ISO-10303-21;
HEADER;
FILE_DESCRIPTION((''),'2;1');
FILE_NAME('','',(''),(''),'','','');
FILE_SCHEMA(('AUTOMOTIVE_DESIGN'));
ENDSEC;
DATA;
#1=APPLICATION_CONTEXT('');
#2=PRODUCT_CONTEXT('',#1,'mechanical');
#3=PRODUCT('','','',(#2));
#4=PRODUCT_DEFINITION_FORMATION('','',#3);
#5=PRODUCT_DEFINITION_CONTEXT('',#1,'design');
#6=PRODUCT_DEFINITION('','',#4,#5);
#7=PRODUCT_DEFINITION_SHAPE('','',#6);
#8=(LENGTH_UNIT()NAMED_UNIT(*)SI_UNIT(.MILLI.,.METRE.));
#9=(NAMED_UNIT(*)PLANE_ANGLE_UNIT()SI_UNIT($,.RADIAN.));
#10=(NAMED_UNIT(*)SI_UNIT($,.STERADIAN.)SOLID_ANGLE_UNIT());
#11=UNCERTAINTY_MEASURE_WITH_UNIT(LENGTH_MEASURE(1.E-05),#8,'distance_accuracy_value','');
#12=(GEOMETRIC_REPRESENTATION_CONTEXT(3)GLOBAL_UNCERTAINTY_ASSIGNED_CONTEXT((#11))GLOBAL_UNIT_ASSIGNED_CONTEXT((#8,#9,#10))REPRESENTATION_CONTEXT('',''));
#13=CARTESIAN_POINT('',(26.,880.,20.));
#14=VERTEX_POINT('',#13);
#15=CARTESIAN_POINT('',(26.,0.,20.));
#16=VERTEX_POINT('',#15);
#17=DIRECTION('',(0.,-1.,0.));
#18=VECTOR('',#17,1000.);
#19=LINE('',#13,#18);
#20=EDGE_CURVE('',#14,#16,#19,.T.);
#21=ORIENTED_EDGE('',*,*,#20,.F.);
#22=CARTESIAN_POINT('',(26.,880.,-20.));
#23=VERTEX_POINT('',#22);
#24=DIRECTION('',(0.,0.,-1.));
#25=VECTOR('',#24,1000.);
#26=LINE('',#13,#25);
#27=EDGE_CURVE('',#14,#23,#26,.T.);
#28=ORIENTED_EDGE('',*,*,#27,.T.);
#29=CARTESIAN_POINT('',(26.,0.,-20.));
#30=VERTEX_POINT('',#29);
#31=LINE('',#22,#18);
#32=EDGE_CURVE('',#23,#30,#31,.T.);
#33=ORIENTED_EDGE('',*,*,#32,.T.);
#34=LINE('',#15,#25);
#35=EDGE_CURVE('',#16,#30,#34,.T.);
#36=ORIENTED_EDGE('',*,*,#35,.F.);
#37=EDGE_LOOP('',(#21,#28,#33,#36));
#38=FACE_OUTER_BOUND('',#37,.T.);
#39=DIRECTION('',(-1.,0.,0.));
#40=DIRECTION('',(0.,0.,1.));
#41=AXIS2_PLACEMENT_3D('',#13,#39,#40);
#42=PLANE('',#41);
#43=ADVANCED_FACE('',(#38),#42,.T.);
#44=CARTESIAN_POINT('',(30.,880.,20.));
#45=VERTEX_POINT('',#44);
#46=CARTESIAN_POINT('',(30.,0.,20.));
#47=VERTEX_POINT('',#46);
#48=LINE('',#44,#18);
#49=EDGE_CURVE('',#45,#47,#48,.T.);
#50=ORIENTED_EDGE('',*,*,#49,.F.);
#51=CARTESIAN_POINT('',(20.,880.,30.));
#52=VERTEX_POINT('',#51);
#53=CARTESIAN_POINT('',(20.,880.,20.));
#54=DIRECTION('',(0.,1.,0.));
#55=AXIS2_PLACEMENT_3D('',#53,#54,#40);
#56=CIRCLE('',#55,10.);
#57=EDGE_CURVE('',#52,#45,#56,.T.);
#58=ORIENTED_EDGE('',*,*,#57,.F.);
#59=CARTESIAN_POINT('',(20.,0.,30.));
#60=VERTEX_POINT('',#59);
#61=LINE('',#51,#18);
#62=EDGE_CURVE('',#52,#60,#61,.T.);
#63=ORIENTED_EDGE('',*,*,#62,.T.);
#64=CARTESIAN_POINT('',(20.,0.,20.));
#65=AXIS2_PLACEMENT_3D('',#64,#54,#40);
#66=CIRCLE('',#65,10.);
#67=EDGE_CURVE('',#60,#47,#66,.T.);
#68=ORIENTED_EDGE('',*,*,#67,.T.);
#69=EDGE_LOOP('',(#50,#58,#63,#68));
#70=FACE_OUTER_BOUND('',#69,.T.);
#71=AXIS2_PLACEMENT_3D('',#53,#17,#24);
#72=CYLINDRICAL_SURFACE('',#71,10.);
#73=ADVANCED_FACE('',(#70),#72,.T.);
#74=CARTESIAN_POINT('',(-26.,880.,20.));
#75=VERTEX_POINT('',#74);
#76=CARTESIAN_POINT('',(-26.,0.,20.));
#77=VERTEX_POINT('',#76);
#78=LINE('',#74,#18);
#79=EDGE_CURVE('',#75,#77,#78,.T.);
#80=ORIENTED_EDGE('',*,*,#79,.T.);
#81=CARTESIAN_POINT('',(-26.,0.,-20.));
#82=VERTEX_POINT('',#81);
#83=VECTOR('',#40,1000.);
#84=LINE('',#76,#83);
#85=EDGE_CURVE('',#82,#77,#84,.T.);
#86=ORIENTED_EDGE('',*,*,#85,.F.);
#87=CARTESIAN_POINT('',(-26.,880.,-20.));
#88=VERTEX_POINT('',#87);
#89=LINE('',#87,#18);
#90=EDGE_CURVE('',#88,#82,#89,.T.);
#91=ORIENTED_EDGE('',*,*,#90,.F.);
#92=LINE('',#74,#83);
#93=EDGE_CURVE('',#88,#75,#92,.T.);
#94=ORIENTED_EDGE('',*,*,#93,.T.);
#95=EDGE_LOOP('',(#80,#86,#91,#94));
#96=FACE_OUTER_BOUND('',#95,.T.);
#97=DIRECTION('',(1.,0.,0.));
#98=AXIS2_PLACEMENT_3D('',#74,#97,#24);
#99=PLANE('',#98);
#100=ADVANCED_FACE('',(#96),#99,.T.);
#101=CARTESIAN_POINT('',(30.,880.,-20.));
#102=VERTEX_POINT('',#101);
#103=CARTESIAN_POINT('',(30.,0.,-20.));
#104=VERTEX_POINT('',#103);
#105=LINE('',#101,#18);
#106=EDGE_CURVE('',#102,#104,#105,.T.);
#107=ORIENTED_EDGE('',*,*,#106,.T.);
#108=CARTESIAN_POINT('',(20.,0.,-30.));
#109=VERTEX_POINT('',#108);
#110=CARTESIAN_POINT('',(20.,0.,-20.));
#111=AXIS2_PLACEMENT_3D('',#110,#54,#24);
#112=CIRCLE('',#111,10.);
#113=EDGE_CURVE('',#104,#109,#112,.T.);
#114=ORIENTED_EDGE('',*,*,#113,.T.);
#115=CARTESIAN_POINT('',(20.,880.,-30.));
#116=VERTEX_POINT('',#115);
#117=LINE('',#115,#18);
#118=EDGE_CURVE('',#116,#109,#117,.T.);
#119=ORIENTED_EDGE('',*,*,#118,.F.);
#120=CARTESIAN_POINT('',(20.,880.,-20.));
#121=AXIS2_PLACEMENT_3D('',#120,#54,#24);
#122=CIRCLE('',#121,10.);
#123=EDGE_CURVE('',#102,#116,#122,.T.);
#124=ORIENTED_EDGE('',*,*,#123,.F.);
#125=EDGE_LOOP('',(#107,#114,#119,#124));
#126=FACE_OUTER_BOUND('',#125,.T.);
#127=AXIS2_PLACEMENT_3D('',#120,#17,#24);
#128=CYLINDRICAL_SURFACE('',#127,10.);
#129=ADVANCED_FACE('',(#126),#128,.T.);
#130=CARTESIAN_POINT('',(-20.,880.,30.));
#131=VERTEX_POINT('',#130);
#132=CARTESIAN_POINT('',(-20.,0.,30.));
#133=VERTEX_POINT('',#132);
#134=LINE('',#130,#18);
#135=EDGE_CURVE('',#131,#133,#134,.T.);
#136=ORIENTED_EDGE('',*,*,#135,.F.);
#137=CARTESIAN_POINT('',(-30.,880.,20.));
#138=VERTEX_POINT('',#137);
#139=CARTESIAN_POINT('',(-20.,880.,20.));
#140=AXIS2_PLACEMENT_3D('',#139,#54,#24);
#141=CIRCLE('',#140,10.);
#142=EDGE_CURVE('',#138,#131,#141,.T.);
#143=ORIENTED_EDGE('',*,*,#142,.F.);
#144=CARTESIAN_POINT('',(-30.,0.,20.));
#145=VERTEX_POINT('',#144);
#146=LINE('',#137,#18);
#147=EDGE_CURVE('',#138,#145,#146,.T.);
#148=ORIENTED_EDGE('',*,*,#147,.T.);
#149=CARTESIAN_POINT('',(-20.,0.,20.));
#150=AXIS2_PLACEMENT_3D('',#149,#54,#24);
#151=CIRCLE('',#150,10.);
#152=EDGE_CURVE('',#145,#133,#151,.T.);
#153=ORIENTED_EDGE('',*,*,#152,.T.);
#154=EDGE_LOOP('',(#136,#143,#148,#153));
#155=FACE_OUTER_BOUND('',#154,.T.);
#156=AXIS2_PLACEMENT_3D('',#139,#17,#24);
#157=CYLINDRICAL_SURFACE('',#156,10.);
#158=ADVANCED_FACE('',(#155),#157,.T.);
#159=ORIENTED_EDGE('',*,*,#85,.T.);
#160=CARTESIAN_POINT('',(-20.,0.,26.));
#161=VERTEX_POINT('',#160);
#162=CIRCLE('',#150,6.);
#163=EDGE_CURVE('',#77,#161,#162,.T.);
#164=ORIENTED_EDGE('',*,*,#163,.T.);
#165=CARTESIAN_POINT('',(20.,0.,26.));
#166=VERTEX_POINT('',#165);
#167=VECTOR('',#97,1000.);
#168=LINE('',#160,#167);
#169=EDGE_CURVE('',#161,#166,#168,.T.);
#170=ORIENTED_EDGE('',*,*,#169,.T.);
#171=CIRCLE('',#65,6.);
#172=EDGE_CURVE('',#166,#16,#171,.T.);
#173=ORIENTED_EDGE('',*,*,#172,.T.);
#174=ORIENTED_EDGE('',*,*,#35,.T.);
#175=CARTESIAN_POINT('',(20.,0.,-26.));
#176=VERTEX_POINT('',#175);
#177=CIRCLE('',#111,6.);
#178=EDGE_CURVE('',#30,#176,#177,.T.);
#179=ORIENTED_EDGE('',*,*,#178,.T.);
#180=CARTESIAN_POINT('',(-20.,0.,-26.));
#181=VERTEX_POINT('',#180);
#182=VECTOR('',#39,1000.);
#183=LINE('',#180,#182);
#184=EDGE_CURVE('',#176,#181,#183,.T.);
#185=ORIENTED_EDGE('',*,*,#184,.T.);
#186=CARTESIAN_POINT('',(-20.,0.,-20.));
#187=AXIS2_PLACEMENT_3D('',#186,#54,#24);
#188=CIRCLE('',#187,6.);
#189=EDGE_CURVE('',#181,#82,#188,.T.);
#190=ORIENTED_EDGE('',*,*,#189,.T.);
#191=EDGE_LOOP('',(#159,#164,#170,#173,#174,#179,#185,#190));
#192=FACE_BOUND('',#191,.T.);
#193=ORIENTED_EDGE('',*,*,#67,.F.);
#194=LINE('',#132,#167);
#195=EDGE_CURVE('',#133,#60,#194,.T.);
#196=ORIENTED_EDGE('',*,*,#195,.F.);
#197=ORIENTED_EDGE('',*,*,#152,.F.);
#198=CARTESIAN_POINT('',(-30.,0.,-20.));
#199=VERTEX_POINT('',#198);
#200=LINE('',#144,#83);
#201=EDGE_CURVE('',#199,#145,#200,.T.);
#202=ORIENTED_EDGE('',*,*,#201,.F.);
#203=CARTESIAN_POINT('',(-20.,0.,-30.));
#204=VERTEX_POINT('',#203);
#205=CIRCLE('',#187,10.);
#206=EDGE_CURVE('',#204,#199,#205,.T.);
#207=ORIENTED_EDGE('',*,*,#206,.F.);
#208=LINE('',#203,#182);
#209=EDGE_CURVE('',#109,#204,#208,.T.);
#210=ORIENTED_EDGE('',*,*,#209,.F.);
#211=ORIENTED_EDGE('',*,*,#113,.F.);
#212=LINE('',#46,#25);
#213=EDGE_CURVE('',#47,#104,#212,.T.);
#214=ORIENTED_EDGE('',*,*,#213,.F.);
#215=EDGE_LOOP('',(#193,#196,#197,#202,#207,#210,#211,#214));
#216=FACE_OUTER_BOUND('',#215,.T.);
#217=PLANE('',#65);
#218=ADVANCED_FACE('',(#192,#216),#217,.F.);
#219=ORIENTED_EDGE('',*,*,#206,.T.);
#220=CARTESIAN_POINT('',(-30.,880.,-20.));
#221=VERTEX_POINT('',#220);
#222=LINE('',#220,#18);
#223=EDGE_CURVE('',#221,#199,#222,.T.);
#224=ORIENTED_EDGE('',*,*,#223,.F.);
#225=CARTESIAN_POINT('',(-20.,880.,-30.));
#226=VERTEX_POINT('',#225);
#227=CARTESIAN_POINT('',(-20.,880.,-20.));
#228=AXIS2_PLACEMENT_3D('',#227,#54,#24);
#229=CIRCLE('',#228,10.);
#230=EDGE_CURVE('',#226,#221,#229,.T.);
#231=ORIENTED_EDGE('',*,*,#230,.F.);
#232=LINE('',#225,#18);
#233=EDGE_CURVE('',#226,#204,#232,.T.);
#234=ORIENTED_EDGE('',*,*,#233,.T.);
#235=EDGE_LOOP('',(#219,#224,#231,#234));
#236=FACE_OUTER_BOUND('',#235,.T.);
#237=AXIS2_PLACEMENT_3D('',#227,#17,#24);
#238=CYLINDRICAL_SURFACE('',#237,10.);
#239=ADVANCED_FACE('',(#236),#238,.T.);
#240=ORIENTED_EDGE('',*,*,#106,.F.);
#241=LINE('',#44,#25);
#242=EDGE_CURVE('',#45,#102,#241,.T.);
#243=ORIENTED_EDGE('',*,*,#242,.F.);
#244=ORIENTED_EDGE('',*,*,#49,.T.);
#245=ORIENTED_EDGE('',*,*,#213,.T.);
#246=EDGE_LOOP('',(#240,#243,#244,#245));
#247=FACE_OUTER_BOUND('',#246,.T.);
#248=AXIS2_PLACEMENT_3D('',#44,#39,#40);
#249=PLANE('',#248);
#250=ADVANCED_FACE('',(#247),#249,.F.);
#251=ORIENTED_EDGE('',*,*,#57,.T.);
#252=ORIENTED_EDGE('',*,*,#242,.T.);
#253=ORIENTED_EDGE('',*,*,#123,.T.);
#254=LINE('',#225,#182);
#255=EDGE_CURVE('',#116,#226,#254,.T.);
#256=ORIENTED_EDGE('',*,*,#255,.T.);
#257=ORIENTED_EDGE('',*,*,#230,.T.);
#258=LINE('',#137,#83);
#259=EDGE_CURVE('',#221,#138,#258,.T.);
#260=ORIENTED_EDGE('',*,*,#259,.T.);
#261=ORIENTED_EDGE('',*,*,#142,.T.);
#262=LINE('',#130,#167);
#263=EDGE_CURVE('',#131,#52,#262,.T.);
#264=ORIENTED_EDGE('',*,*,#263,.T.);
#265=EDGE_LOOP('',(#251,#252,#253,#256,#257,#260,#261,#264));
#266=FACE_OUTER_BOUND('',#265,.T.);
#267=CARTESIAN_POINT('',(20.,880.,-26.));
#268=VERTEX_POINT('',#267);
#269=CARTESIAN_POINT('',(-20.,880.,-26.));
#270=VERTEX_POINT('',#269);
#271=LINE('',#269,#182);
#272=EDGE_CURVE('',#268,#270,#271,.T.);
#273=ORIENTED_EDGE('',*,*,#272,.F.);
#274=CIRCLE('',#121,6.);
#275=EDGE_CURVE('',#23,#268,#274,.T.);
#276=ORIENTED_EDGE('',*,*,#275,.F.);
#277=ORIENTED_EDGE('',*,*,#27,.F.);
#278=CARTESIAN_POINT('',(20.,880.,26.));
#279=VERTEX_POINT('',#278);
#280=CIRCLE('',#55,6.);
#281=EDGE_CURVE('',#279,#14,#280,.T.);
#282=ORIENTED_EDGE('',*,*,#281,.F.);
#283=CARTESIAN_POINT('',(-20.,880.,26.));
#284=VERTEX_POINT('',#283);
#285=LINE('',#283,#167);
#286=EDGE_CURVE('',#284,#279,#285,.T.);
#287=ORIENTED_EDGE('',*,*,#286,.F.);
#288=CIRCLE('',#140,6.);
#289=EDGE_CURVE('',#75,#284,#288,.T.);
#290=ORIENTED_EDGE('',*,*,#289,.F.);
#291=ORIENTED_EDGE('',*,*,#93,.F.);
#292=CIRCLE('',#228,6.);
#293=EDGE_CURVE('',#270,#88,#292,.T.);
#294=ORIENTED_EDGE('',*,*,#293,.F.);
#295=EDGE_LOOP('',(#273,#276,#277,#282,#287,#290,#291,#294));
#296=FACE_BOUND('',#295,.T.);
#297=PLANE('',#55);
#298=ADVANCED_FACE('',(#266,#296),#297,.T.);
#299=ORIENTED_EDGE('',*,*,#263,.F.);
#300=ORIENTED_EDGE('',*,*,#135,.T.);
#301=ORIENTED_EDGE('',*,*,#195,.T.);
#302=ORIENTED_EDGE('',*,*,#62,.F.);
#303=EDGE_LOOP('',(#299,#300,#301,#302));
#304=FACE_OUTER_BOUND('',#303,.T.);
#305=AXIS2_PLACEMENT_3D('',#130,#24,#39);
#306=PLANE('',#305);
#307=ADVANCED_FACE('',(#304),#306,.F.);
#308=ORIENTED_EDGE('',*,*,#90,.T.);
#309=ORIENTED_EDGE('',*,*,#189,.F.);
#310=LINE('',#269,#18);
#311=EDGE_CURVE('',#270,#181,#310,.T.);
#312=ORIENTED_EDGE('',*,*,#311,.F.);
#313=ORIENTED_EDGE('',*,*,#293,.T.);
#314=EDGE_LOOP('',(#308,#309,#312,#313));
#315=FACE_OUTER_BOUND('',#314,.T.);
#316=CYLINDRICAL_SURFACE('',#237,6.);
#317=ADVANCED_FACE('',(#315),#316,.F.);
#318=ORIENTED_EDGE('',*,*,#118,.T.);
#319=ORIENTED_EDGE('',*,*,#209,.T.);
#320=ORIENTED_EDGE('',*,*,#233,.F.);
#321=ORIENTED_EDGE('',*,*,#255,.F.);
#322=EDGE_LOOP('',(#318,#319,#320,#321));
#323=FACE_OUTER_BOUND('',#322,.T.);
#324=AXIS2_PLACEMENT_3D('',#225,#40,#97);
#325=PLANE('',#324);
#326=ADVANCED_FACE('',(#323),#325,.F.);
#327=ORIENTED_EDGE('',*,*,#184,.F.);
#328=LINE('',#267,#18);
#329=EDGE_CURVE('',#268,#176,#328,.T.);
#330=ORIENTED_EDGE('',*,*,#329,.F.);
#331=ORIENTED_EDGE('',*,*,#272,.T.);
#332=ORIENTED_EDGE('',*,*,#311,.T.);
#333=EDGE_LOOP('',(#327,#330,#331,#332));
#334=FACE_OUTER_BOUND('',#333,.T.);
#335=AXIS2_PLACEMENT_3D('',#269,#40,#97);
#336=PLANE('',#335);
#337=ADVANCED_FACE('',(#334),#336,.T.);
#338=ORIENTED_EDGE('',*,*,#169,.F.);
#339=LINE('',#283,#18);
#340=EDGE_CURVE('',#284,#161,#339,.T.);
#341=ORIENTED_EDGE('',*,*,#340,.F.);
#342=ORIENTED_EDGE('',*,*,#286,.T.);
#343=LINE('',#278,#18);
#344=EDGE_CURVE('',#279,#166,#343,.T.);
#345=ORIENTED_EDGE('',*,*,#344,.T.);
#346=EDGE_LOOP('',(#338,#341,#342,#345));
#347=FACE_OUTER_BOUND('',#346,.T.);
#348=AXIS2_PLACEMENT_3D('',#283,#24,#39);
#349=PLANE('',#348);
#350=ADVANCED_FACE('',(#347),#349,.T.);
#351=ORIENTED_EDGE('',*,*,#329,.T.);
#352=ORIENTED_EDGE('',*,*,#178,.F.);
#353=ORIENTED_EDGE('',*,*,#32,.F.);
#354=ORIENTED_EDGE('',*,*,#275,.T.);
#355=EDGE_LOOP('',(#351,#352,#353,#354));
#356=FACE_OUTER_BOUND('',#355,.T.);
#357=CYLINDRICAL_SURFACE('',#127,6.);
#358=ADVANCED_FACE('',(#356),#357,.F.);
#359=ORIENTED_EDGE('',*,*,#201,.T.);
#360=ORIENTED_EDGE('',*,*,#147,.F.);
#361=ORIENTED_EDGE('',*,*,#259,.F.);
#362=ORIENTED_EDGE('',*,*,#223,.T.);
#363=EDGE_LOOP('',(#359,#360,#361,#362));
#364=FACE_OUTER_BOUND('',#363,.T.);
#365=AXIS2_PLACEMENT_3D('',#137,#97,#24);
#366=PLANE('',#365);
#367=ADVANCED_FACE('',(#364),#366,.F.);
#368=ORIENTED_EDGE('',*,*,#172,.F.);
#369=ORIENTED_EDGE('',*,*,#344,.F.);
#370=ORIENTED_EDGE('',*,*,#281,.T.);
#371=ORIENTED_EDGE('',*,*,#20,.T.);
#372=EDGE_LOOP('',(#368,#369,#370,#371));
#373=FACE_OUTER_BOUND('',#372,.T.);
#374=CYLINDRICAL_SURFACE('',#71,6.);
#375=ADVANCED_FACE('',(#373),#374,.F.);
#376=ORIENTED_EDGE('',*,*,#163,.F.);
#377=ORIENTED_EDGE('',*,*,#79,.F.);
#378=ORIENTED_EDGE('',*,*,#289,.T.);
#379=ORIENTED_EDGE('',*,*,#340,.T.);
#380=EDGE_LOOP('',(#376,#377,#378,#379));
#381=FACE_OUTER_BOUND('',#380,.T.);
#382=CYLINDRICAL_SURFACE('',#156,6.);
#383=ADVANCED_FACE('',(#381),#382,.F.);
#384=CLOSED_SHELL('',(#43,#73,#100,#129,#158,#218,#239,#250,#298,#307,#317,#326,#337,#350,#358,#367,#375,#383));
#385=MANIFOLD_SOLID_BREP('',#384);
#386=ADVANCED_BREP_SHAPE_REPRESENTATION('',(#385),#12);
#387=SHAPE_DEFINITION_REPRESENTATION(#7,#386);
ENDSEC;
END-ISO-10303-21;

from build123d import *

# Parameters (mm, degrees)
BOSS_EXTRUDE1_DEPTH = 880


with BuildPart() as part:
    # Sketch1 → Boss-Extrude1 (new body)
    with BuildSketch(Plane(origin=(0, 0, 0), x_dir=(1, 0, 0), z_dir=(0, 1, 0))):
        with BuildLine():
            Line((-20, -30), (20, -30))
            ThreePointArc((20, -30), (27.071067812, -27.071067812), (30, -20))
            Line((30, -20), (30, 20))
            ThreePointArc((30, 20), (27.071067812, 27.071067812), (20, 30))
            Line((20, 30), (-20, 30))
            ThreePointArc((-20, 30), (-27.071067812, 27.071067812), (-30, 20))
            Line((-30, 20), (-30, -20))
            ThreePointArc((-30, -20), (-27.071067812, -27.071067812), (-20, -30))
        make_face()
        with BuildLine():
            Line((-26, -20), (-26, 20))
            ThreePointArc((-26, 20), (-24.242640687, 24.242640687), (-20, 26))
            Line((-20, 26), (20, 26))
            ThreePointArc((20, 26), (24.242640687, 24.242640687), (26, 20))
            Line((26, 20), (26, -20))
            ThreePointArc((26, -20), (24.242640687, -24.242640687), (20, -26))
            Line((20, -26), (-20, -26))
            ThreePointArc((-20, -26), (-24.242640687, -24.242640687), (-26, -20))
        make_face(mode=Mode.SUBTRACT)
    extrude(amount=BOSS_EXTRUDE1_DEPTH)


solid = part.part
